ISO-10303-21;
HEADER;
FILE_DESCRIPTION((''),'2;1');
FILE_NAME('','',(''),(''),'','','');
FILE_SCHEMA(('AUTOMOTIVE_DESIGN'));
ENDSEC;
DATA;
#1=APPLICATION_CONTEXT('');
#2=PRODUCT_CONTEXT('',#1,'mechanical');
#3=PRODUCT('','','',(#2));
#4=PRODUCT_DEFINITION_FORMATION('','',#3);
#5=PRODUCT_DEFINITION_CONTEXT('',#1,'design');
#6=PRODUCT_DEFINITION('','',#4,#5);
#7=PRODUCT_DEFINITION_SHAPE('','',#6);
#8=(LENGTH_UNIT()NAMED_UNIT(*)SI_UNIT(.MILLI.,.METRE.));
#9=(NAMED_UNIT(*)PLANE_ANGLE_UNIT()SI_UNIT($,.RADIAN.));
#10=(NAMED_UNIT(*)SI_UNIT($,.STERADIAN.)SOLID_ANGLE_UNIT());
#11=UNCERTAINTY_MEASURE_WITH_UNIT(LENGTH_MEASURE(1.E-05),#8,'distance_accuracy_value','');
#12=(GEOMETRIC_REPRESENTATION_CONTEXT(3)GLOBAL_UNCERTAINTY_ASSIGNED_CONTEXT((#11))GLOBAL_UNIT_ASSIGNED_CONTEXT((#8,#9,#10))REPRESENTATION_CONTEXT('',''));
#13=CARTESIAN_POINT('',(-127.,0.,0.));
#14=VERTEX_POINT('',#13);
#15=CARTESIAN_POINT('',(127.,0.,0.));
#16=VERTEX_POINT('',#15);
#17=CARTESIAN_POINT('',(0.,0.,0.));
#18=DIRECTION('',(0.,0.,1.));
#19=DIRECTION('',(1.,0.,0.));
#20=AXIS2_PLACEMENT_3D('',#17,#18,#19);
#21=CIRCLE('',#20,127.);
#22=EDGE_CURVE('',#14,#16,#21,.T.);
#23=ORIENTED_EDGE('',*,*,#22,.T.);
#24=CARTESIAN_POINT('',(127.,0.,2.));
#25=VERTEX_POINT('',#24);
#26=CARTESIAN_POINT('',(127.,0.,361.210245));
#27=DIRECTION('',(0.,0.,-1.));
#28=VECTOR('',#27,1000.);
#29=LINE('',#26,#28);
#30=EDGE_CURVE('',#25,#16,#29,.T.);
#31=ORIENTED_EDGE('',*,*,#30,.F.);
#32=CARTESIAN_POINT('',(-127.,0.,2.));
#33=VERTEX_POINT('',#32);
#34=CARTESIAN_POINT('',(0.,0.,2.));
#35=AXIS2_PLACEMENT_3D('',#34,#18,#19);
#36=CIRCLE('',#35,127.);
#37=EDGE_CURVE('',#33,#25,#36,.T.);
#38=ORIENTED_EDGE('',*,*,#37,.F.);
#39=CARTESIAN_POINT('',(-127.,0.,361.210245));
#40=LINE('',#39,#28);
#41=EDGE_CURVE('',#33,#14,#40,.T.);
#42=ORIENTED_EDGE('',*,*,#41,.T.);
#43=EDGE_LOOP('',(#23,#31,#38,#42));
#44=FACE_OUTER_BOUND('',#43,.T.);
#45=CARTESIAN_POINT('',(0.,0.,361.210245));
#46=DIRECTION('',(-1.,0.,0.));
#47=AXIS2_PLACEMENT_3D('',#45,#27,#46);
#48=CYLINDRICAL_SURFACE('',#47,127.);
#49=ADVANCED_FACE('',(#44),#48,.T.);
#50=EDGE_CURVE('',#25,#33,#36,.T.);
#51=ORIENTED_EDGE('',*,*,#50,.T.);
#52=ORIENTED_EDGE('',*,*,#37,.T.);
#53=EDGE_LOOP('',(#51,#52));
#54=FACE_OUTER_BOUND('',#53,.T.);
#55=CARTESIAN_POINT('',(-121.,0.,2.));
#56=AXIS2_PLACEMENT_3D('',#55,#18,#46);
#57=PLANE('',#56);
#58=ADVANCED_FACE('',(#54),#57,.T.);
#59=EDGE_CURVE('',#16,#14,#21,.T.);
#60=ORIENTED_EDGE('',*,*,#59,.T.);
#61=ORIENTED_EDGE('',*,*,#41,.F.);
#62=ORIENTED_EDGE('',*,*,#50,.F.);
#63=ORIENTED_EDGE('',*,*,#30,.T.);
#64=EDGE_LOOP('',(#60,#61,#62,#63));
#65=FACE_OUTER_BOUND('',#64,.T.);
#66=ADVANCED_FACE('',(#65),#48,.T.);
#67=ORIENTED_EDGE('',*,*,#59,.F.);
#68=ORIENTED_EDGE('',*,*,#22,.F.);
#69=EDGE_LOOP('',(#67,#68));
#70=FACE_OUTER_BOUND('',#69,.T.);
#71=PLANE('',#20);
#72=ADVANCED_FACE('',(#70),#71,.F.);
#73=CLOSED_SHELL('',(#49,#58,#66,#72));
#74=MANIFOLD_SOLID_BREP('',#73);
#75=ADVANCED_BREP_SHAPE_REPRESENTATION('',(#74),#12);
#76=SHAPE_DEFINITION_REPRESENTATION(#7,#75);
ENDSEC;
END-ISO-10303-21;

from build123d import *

# Parameters (mm, degrees)
SKETCH1_R           = 127
BOSS_EXTRUDE1_DEPTH = 2


with BuildPart() as part:
    # Sketch1 → Boss-Extrude1 (new body)
    with BuildSketch(Plane.XY):
        Circle(SKETCH1_R)
    extrude(amount=BOSS_EXTRUDE1_DEPTH)


solid = part.part
